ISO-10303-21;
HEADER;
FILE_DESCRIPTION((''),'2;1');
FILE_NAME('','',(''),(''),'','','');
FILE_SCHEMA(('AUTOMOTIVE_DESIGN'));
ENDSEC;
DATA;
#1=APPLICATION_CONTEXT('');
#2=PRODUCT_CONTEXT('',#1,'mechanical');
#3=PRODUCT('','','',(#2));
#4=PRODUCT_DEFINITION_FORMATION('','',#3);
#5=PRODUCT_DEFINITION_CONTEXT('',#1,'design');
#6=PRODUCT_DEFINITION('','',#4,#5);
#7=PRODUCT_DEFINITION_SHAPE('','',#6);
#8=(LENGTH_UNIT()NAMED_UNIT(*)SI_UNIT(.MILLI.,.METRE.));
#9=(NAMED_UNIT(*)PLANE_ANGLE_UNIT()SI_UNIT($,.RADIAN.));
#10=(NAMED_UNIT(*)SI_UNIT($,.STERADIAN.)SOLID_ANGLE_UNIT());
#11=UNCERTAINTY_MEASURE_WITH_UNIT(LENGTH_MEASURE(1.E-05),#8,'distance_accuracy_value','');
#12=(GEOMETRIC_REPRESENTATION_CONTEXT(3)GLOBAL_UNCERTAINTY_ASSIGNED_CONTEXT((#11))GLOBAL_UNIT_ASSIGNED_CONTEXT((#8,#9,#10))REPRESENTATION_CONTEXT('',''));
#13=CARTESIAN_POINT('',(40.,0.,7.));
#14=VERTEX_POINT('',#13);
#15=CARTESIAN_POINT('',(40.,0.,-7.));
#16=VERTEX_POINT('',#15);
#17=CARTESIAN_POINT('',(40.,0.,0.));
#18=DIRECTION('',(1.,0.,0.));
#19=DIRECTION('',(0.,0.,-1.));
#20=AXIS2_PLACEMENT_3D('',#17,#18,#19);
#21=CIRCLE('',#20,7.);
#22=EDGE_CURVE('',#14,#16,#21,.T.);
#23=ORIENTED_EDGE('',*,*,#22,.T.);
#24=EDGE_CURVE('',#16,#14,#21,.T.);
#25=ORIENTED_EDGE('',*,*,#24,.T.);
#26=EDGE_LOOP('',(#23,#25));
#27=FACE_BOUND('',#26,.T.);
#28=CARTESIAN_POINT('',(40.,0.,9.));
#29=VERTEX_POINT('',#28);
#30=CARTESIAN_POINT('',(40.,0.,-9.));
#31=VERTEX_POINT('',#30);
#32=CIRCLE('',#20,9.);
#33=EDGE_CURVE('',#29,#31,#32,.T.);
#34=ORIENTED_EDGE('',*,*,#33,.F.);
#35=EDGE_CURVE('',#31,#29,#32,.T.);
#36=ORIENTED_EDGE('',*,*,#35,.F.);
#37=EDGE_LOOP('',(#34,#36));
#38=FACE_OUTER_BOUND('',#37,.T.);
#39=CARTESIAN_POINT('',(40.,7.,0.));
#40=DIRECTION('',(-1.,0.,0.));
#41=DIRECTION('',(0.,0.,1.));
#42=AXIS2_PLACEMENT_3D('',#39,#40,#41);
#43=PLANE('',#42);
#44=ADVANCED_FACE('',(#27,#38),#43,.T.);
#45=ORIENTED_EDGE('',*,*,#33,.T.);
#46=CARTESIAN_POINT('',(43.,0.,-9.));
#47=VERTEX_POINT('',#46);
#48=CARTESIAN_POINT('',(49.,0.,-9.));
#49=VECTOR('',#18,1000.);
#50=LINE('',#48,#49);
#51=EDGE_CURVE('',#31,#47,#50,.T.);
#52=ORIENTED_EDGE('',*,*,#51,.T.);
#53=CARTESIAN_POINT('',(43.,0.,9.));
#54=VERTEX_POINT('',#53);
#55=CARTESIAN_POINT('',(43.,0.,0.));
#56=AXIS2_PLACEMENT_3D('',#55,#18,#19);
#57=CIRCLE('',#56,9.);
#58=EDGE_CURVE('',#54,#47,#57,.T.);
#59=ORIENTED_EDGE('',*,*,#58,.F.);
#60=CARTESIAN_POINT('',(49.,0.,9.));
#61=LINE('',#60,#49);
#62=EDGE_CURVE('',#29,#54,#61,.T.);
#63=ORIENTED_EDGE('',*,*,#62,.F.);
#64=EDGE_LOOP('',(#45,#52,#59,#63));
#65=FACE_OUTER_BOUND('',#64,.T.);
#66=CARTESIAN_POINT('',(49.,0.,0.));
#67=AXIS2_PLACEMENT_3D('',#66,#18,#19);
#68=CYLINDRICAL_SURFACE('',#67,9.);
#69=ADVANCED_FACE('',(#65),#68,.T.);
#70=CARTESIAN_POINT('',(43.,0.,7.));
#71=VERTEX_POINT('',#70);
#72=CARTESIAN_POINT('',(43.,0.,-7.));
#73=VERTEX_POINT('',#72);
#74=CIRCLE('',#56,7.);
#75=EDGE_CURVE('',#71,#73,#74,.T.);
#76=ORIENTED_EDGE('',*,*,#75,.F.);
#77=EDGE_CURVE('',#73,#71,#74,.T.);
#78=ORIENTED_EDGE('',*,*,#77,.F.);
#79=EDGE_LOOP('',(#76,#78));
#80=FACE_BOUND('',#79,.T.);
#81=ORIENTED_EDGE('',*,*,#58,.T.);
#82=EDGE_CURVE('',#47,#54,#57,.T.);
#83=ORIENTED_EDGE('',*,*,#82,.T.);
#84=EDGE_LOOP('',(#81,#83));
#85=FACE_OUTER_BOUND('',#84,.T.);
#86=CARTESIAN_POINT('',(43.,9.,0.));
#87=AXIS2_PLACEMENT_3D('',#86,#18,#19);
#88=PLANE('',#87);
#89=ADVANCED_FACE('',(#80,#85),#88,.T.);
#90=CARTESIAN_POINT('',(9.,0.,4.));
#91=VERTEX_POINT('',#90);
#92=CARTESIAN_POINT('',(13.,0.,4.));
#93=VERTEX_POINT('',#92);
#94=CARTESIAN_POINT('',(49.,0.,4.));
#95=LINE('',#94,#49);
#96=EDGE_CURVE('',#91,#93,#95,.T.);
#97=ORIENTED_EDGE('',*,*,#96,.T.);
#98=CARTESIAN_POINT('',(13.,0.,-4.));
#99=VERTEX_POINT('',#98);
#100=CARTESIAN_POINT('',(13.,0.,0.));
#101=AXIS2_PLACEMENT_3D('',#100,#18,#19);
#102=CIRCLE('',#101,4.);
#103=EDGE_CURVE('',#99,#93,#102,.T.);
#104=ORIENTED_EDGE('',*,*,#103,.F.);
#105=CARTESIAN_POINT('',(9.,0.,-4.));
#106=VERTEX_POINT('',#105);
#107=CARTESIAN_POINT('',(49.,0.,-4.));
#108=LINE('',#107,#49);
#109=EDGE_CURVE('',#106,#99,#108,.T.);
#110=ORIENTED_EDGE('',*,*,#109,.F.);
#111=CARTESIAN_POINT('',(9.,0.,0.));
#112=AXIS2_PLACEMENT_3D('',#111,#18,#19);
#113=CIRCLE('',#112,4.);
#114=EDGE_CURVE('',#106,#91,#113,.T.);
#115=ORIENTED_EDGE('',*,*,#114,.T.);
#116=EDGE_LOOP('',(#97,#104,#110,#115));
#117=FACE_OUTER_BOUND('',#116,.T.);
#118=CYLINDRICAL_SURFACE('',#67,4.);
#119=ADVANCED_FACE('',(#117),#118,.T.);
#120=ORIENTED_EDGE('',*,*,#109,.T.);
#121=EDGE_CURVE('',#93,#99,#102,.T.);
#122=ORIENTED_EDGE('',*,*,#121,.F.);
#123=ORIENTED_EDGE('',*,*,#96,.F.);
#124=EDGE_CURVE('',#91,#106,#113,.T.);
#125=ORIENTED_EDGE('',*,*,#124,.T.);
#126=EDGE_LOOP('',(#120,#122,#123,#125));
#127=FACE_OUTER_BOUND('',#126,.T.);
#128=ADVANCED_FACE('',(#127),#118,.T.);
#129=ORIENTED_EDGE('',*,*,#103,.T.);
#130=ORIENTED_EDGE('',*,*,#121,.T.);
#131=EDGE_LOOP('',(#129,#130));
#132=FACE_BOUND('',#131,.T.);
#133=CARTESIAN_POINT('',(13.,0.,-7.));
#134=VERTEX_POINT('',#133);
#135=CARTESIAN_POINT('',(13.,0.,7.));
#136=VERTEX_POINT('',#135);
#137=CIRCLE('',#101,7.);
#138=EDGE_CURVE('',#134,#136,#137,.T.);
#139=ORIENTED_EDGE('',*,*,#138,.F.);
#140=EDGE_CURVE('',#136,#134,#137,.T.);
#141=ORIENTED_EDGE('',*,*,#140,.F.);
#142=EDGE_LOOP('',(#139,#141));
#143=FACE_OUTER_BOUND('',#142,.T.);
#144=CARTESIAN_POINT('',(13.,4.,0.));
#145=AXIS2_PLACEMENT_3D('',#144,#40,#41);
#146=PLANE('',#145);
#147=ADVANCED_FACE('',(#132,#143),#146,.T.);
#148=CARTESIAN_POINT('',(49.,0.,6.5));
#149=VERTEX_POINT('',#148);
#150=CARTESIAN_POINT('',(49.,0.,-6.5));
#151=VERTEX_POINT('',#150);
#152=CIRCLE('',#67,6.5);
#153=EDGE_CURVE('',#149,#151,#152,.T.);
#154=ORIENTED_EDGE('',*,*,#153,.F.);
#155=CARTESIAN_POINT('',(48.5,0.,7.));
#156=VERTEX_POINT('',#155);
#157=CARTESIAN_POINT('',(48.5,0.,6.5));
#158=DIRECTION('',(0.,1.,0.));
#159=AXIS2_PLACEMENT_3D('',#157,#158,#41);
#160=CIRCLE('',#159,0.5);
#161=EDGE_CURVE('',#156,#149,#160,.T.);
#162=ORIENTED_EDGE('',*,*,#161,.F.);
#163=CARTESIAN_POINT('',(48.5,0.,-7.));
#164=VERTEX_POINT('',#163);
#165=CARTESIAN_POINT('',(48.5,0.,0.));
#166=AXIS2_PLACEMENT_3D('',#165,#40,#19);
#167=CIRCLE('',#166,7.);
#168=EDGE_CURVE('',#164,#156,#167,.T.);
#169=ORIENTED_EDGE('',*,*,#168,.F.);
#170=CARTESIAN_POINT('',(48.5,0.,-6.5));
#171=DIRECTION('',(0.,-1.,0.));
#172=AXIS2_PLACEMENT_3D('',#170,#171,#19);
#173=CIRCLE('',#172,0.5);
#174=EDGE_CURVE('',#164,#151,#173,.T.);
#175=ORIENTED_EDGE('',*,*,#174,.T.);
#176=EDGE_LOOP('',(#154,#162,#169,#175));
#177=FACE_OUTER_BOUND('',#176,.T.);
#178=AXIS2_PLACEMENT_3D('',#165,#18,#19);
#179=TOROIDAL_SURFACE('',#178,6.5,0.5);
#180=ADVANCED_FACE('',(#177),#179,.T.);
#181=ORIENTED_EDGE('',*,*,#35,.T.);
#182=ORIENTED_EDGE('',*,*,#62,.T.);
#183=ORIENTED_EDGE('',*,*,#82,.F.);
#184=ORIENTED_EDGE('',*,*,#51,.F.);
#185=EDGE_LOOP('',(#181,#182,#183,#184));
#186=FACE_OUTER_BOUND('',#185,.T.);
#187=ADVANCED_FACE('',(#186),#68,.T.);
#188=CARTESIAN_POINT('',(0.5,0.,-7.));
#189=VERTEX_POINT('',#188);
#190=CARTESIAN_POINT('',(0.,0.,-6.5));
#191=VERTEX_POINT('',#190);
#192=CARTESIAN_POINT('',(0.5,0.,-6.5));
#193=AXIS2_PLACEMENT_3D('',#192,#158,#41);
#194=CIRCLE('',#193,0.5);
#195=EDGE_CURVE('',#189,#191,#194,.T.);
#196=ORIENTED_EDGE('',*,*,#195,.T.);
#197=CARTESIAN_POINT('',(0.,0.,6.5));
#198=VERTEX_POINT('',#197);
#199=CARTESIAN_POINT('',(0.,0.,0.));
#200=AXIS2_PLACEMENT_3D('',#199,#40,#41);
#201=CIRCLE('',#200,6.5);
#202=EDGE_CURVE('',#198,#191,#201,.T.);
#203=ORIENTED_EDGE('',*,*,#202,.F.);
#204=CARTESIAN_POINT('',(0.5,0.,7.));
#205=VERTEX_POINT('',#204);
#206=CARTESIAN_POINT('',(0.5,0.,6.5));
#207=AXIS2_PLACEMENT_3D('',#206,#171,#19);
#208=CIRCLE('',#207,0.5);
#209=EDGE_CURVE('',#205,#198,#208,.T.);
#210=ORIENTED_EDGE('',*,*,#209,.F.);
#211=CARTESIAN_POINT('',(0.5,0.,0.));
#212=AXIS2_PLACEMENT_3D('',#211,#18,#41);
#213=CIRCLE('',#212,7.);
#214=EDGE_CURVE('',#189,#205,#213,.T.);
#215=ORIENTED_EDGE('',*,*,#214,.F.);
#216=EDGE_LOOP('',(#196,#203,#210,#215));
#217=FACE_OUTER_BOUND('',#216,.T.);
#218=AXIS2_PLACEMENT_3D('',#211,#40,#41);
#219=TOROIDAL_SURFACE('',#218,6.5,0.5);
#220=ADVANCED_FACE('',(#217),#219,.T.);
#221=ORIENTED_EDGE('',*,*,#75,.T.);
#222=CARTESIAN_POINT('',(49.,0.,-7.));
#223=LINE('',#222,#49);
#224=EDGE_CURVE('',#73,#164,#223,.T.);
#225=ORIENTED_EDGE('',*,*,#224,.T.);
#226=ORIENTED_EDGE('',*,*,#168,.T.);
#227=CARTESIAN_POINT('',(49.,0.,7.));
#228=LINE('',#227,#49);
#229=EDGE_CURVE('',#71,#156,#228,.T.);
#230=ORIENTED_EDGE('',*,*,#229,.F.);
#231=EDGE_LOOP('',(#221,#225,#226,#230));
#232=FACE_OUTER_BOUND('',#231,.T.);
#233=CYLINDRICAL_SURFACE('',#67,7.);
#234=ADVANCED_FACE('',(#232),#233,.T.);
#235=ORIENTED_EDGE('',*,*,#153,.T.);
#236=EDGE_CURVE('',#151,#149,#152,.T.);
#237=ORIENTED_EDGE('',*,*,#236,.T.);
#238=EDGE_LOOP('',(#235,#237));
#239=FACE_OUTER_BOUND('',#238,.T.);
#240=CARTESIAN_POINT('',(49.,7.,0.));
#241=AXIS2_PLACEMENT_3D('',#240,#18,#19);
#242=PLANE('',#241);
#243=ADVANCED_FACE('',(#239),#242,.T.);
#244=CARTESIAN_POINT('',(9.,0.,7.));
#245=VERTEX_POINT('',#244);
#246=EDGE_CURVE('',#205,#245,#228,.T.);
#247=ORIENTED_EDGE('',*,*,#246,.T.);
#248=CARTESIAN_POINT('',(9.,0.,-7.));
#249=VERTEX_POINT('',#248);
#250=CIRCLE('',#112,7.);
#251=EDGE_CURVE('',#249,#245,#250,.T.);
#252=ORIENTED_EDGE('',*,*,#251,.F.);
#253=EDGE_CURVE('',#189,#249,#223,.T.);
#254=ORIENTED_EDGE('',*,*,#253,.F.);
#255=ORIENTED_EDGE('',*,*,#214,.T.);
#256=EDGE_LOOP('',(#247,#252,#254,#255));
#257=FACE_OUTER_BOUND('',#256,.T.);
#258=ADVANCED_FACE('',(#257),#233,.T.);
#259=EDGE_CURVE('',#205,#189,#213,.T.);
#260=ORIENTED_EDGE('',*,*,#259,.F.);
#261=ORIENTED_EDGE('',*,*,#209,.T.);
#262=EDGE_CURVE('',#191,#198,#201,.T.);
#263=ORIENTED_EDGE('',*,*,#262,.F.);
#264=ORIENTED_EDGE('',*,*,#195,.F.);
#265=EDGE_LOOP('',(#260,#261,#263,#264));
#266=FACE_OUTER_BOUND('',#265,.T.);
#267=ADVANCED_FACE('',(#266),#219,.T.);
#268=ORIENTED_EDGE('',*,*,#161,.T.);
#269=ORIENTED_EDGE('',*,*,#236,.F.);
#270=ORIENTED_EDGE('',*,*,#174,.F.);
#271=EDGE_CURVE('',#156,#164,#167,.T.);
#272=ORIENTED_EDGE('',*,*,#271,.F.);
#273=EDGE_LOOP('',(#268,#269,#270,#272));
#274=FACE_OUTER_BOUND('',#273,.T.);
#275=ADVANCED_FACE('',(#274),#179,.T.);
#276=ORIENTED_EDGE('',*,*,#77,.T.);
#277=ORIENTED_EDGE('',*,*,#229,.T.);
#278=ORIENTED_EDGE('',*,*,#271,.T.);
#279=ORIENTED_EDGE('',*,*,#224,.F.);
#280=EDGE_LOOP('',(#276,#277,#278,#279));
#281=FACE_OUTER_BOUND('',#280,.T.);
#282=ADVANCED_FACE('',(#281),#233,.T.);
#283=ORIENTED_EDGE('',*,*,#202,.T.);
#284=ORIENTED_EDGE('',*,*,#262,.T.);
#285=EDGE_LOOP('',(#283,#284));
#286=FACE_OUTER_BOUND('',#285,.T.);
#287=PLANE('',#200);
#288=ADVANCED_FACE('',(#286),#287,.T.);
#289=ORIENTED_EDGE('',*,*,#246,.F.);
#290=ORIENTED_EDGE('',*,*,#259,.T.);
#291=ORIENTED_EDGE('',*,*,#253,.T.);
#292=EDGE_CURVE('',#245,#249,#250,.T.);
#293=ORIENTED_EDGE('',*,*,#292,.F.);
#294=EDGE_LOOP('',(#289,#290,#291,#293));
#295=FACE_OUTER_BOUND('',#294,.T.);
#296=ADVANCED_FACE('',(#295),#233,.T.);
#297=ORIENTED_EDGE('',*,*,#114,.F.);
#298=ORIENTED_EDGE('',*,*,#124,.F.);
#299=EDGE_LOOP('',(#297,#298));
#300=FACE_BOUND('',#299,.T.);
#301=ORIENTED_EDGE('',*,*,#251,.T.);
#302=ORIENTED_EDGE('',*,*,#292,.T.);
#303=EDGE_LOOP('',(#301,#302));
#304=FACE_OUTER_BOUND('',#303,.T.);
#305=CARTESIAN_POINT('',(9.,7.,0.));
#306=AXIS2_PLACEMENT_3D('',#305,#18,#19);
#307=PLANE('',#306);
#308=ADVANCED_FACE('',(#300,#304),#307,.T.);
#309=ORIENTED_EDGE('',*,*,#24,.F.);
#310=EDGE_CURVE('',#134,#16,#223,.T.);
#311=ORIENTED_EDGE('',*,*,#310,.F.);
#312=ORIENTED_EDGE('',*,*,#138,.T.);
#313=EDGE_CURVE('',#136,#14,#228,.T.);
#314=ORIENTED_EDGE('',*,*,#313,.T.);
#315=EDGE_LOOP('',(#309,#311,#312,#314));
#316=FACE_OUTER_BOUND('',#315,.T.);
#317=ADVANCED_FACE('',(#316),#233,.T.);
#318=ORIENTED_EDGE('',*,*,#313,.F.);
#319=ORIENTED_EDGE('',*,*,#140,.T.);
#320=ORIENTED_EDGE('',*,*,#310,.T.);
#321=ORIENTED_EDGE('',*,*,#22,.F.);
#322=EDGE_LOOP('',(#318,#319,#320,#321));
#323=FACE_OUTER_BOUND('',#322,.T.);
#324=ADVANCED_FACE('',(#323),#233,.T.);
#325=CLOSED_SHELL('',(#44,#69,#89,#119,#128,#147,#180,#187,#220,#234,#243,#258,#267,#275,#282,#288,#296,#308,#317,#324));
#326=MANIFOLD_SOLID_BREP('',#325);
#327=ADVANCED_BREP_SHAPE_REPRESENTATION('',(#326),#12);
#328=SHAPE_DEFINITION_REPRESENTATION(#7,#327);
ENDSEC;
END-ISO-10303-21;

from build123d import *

# Parameters (mm, degrees)
FILLET1_R = 0.5


with BuildPart() as part:
    # Sketch1 → Revolve1 (revolve)
    with BuildSketch(Plane.XY, mode=Mode.PRIVATE) as revolve1_sk:
        Polygon((0, 0), (0, 7), (9, 7), (9, 4), (13, 4), (13, 7), (40, 7), (40, 9), (43, 9), (43, 7), (49, 7), (49, 0), align=None)
    revolve(revolve1_sk.sketch.rotate(Axis((49, 0, 0), (-1, 0, 0)), 90), axis=Axis((49, 0, 0), (-1, 0, 0)))

    # Fillet1
    fillet1_edges = [part.edges().sort_by_distance(p)[0] for p in [
        (0, 0, 7),
        (49, 0, 7),
    ]]
    fillet(fillet1_edges, radius=FILLET1_R)


solid = part.part
